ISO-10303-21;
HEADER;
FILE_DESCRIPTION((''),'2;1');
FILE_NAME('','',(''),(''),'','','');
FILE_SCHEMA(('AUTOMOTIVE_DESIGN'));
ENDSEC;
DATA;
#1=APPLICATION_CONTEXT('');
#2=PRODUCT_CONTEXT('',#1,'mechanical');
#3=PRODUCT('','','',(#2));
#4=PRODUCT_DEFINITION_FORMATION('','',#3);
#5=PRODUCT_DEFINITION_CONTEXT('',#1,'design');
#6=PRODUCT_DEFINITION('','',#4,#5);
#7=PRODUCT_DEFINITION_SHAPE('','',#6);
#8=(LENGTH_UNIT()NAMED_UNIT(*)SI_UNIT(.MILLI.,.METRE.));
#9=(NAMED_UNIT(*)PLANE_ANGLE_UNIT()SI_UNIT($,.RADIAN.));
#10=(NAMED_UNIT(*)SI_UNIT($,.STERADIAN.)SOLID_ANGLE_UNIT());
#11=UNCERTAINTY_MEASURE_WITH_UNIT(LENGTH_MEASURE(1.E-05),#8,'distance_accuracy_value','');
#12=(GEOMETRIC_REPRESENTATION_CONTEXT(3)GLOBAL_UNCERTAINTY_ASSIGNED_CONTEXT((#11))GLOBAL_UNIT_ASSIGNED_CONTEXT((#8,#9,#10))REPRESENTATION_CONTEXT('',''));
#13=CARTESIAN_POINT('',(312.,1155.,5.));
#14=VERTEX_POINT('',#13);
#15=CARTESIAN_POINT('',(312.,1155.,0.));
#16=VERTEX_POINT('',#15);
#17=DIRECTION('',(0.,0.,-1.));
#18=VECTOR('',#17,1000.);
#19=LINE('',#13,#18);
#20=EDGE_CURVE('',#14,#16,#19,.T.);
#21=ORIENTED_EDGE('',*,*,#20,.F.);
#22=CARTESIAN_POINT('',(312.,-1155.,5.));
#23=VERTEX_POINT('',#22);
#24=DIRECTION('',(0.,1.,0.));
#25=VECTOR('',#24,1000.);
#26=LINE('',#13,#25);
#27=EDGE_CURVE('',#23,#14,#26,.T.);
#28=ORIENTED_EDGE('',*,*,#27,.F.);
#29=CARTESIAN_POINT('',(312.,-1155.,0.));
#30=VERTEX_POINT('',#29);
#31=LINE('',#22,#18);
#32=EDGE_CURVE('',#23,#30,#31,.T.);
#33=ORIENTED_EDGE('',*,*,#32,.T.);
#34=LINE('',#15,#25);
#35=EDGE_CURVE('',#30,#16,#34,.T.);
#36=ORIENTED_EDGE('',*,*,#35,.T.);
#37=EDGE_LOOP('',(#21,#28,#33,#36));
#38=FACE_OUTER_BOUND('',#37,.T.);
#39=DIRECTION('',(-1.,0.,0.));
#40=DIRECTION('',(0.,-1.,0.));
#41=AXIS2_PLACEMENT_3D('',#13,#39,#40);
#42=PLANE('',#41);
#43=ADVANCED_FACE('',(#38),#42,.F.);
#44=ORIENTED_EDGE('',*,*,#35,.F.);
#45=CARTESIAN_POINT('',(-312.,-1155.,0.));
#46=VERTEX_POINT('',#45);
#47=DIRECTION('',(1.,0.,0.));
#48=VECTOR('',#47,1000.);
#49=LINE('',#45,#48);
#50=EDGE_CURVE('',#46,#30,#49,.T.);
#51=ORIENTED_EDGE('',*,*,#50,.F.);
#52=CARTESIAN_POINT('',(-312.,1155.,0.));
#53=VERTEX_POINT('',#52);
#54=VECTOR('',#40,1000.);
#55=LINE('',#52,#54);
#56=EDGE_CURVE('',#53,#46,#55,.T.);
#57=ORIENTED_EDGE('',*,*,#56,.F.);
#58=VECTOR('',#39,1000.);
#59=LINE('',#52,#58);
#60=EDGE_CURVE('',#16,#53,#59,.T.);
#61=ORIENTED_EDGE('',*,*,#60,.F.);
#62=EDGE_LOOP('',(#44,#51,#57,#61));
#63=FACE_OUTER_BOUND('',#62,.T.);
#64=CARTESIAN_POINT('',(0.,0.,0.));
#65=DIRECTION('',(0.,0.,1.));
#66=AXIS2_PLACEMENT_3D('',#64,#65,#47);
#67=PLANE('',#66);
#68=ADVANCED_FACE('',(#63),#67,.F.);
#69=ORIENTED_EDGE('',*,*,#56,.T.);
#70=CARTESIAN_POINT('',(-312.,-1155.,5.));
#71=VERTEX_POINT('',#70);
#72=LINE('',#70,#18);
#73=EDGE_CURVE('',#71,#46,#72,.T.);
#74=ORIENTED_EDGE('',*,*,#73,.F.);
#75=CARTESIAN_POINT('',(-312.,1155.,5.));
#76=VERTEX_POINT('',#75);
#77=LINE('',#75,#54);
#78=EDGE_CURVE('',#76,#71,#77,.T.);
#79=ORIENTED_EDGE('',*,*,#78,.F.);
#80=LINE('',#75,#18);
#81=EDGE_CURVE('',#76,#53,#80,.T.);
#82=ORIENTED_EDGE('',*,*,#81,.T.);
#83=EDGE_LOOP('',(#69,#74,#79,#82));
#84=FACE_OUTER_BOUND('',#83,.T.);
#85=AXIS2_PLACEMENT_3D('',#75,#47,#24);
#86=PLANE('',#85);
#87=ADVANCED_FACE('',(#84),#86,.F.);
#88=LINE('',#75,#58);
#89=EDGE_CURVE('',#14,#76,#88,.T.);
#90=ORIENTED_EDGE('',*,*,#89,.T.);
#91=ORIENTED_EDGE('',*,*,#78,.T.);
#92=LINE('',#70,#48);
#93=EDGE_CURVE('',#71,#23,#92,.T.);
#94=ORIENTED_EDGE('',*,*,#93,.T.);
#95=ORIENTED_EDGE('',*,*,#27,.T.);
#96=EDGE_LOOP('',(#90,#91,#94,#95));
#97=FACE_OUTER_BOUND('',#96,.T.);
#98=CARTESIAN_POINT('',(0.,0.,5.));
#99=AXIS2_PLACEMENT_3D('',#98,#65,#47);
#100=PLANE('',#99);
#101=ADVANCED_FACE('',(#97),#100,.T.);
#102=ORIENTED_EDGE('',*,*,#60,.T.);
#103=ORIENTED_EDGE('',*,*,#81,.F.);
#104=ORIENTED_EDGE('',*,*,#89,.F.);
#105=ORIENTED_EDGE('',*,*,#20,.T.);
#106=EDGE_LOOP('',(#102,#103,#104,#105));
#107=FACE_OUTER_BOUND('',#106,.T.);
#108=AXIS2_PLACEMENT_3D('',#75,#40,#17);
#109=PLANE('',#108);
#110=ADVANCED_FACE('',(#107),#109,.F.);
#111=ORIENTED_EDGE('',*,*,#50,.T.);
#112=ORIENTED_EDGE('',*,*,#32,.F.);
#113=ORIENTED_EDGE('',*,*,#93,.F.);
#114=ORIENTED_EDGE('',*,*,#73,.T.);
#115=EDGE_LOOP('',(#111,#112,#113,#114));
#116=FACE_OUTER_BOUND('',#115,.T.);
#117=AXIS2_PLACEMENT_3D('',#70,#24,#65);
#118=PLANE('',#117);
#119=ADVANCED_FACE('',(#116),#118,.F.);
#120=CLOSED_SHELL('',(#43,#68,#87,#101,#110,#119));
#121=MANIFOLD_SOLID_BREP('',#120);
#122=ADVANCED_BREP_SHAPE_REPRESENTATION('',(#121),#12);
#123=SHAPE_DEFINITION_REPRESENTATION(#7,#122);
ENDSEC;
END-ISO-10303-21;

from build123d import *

# Parameters (mm, degrees)
SKETCH_1_W      = 624
SKETCH_1_H      = 2310
EXTRUDE_1_DEPTH = 5


with BuildPart() as part:
    # 草图1 → 凸台-拉伸1 (new body)
    with BuildSketch(Plane.XY):
        Rectangle(SKETCH_1_W, SKETCH_1_H)
    extrude(amount=EXTRUDE_1_DEPTH)


solid = part.part
